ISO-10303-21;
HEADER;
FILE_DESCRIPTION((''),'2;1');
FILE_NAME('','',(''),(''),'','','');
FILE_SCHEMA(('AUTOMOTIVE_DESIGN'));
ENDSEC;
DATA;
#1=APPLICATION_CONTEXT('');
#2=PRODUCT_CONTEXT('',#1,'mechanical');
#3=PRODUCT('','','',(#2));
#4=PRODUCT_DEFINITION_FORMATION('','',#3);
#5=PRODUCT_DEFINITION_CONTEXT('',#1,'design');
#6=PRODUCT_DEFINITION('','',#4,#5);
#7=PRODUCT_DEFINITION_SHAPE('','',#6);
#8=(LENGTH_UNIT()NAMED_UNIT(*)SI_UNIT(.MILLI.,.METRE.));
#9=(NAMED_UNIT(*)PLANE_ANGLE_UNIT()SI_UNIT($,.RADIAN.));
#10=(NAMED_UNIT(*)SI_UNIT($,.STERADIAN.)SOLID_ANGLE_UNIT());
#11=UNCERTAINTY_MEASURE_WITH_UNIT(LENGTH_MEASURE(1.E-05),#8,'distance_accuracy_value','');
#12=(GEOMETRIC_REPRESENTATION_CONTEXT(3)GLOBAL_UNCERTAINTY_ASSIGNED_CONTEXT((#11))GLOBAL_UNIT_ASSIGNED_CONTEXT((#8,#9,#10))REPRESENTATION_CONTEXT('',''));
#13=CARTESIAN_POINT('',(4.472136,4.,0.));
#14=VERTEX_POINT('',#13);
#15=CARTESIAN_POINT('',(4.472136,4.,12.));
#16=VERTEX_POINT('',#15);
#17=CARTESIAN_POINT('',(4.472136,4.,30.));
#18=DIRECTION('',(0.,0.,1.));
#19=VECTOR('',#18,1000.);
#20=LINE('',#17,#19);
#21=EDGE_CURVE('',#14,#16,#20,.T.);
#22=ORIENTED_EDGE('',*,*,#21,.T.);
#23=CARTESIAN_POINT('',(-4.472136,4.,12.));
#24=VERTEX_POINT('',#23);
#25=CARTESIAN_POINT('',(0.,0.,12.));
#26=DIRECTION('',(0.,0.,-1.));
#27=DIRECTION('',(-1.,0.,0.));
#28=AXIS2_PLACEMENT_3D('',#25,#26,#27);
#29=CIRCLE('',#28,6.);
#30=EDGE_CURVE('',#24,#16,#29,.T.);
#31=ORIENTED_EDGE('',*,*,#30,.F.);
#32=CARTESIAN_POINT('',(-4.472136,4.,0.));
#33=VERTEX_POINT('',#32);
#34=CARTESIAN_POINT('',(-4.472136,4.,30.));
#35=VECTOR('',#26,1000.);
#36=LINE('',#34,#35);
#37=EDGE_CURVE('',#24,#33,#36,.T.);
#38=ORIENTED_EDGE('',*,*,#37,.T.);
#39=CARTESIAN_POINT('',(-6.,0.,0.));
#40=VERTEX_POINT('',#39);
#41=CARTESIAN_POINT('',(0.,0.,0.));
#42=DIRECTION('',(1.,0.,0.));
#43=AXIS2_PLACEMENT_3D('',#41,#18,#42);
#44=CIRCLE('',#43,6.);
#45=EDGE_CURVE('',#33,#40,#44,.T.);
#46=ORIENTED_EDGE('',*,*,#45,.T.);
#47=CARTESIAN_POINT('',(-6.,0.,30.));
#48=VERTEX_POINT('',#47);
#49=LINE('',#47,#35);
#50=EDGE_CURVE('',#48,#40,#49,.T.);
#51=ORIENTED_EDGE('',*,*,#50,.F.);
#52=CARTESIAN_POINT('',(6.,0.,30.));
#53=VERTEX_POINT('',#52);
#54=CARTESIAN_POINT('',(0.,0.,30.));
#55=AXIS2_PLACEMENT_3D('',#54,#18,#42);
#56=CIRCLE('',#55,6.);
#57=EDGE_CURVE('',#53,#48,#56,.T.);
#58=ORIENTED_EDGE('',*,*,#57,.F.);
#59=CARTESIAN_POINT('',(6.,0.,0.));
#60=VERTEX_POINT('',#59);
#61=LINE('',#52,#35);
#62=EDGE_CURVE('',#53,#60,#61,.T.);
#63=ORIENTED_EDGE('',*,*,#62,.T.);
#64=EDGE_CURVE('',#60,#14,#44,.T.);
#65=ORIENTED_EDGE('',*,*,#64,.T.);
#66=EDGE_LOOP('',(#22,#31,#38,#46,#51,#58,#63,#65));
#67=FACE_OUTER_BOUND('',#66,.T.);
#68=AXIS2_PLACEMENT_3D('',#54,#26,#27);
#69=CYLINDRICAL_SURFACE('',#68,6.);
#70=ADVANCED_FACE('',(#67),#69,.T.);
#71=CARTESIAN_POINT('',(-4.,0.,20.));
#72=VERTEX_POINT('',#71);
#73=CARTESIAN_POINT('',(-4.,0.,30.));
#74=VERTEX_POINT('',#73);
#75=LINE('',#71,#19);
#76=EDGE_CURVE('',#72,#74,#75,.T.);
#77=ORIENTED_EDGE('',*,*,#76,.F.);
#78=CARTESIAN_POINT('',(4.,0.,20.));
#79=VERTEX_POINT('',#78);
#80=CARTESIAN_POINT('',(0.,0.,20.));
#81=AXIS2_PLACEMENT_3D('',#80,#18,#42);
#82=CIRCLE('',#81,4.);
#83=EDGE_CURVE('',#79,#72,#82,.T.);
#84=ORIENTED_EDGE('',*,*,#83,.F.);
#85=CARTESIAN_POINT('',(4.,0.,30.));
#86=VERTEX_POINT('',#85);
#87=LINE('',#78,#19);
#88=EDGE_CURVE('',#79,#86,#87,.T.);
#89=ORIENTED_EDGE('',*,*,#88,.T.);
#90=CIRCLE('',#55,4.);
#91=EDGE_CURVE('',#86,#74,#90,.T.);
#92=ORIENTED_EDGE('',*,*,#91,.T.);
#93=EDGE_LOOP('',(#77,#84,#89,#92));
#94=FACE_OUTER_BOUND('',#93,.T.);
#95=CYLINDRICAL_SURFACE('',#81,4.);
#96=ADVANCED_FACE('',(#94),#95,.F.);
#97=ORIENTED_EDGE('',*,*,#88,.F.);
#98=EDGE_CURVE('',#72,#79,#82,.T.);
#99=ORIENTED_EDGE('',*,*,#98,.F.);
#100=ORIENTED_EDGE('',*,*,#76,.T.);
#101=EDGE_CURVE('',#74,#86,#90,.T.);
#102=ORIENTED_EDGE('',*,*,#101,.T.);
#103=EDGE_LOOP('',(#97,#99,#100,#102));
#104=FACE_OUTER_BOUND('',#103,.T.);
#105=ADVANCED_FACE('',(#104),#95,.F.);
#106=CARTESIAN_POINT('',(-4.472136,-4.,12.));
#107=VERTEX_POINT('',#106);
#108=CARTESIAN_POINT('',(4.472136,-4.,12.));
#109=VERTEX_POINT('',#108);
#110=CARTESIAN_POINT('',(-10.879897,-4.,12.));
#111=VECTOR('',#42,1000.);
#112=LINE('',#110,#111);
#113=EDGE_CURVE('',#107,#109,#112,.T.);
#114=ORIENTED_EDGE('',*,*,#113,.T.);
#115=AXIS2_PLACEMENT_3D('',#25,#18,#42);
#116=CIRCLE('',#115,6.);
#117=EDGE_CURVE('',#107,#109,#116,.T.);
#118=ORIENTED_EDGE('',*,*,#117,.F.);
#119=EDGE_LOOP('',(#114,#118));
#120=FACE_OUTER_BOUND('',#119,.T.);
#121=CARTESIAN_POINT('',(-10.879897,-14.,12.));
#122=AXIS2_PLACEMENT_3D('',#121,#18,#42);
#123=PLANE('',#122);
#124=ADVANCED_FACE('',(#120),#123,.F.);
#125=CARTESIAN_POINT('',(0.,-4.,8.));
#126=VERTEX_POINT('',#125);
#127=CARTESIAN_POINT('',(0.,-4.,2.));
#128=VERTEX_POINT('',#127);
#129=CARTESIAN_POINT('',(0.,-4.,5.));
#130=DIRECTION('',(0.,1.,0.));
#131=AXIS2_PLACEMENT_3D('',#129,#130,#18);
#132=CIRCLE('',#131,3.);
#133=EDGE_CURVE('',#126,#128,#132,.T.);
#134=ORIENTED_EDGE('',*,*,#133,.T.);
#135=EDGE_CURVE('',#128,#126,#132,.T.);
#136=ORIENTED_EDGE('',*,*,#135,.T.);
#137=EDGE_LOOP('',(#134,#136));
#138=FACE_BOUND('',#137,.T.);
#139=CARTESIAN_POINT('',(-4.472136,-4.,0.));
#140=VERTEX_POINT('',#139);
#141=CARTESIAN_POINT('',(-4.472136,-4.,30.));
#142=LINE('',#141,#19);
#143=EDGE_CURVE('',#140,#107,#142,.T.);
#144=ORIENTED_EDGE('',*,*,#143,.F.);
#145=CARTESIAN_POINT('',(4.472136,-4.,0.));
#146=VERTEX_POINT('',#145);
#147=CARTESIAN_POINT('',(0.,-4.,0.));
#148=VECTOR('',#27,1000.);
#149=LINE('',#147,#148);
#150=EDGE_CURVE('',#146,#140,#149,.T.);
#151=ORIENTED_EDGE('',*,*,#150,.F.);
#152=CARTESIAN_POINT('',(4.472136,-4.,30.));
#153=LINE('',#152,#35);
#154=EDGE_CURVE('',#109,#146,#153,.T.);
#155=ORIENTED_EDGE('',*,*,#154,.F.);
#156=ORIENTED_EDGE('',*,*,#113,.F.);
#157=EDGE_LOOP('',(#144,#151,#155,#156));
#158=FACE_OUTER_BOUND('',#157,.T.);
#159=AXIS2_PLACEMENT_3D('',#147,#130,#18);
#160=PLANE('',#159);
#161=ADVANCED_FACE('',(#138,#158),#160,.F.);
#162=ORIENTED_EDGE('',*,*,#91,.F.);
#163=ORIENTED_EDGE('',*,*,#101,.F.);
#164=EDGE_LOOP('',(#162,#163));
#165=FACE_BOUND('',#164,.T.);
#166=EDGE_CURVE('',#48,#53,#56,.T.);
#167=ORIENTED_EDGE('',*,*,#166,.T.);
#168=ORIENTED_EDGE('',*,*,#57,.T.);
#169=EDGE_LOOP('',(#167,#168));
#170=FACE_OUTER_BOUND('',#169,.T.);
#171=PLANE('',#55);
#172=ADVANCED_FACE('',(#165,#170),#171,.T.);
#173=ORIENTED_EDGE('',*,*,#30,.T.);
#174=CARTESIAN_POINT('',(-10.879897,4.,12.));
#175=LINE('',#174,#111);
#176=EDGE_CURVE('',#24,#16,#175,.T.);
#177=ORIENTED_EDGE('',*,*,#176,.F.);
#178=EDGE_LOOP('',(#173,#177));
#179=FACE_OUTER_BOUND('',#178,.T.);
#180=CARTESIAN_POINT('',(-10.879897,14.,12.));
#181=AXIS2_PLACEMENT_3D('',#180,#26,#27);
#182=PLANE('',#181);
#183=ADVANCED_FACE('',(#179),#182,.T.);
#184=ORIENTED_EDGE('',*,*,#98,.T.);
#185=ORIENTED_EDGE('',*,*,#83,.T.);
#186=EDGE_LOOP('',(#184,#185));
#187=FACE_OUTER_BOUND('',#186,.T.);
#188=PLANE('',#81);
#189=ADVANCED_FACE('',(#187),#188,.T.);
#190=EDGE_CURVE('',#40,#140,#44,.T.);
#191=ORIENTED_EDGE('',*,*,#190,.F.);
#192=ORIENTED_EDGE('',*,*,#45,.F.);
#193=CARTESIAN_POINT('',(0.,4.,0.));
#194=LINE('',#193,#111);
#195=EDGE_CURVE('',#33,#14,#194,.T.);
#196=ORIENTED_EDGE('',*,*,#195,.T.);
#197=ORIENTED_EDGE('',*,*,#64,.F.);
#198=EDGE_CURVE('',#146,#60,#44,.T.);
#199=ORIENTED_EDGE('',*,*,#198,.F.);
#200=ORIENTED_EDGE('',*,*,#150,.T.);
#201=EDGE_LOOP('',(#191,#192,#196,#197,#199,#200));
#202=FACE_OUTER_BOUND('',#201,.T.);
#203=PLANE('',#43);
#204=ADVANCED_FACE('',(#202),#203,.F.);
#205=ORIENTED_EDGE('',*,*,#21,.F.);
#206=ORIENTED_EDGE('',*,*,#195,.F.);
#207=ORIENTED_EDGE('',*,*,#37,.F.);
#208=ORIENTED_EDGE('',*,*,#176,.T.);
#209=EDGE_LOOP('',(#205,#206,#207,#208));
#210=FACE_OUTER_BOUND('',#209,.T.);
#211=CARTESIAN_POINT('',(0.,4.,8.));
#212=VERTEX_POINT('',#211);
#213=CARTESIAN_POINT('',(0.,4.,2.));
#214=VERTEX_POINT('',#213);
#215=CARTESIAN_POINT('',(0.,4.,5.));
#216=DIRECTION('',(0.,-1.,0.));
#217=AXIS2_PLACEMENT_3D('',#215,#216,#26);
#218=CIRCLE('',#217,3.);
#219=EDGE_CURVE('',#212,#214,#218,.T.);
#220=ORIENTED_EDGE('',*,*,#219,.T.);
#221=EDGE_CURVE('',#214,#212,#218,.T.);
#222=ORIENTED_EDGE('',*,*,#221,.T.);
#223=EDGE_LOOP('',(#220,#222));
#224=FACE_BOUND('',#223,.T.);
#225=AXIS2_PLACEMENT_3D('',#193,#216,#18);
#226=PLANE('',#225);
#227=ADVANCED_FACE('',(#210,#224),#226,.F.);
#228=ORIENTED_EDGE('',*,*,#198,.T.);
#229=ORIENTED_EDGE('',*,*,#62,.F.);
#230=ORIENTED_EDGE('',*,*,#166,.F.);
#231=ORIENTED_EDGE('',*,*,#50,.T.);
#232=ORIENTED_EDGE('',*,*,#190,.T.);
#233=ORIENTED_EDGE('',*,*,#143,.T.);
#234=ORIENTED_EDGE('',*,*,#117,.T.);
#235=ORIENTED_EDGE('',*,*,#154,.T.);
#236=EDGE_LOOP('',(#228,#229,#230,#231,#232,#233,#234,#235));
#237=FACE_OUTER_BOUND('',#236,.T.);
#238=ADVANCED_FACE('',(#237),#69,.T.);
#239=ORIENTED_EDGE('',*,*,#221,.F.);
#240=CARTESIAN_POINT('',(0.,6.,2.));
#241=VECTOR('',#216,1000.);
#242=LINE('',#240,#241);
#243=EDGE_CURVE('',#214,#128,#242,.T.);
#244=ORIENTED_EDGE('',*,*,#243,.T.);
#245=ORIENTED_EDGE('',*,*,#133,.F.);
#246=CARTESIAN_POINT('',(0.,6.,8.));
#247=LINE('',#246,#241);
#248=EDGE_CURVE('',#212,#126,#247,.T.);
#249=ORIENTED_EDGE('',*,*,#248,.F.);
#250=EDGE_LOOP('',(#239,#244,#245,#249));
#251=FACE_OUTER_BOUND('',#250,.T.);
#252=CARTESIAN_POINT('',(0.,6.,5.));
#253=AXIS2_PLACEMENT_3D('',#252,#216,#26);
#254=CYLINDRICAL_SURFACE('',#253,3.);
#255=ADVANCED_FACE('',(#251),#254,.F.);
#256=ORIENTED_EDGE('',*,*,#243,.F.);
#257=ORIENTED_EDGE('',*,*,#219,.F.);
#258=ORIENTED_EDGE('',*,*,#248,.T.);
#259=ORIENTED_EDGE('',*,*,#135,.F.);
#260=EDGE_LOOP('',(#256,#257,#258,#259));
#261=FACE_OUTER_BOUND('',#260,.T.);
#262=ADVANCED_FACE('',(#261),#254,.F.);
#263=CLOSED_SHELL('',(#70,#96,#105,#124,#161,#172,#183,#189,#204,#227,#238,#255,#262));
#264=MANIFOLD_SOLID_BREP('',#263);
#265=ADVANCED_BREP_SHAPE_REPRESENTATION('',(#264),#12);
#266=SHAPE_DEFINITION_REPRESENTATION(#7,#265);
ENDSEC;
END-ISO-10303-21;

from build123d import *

# Parameters (mm, degrees)
SKETCH1_R               = 6
BOSS_EXTRUDE1_DEPTH     = 30
CUT_EXTRUDE1_START      = -4
SKETCH2_W               = 22.463140108
SKETCH2_H               = 15.309140372
CUT_EXTRUDE1_DEPTH      = 10
CUT_EXTRUDE2_DEPTH      = 33.186953879
CUT_EXTRUDE2_DEPTH_BACK = 33.186953879
SKETCH3_R               = 3
SKETCH4_R               = 4
CUT_EXTRUDE3_DEPTH      = 10


with BuildPart() as part:
    # Sketch1 → Boss-Extrude1 (new body)
    with BuildSketch(Plane.XY):
        Circle(SKETCH1_R)
    extrude(amount=BOSS_EXTRUDE1_DEPTH)

    # Sketch2 → Cut-Extrude1 (cut)
    with BuildSketch(Plane(origin=(0, 0, 0), x_dir=(1, 0, 0), z_dir=(0, 1, 0)).offset(CUT_EXTRUDE1_START)):
        with Locations((0.351673426, -4.345429814)):
            Rectangle(SKETCH2_W, SKETCH2_H)
    cut_extrude1 = extrude(amount=-CUT_EXTRUDE1_DEPTH, mode=Mode.SUBTRACT)

    # Mirror1: Cut-Extrude1 across plane
    add(cut_extrude1.mirror(Plane.ZX), mode=Mode.SUBTRACT)

    # Sketch3 → Cut-Extrude2 (cut, two sides: drawn at the far end of the back side and taken through both)
    with BuildSketch(Plane.XZ.offset(4).offset(-CUT_EXTRUDE2_DEPTH_BACK)):
        with Locations(Location((0, 5, 0), (0, 0, 270))):
            Circle(SKETCH3_R)
    extrude(amount=CUT_EXTRUDE2_DEPTH + CUT_EXTRUDE2_DEPTH_BACK, mode=Mode.SUBTRACT)

    # Sketch4 → Cut-Extrude3 (cut)
    with BuildSketch(Plane.XY.offset(30)):
        Circle(SKETCH4_R)
    extrude(amount=-CUT_EXTRUDE3_DEPTH, mode=Mode.SUBTRACT)


solid = part.part
